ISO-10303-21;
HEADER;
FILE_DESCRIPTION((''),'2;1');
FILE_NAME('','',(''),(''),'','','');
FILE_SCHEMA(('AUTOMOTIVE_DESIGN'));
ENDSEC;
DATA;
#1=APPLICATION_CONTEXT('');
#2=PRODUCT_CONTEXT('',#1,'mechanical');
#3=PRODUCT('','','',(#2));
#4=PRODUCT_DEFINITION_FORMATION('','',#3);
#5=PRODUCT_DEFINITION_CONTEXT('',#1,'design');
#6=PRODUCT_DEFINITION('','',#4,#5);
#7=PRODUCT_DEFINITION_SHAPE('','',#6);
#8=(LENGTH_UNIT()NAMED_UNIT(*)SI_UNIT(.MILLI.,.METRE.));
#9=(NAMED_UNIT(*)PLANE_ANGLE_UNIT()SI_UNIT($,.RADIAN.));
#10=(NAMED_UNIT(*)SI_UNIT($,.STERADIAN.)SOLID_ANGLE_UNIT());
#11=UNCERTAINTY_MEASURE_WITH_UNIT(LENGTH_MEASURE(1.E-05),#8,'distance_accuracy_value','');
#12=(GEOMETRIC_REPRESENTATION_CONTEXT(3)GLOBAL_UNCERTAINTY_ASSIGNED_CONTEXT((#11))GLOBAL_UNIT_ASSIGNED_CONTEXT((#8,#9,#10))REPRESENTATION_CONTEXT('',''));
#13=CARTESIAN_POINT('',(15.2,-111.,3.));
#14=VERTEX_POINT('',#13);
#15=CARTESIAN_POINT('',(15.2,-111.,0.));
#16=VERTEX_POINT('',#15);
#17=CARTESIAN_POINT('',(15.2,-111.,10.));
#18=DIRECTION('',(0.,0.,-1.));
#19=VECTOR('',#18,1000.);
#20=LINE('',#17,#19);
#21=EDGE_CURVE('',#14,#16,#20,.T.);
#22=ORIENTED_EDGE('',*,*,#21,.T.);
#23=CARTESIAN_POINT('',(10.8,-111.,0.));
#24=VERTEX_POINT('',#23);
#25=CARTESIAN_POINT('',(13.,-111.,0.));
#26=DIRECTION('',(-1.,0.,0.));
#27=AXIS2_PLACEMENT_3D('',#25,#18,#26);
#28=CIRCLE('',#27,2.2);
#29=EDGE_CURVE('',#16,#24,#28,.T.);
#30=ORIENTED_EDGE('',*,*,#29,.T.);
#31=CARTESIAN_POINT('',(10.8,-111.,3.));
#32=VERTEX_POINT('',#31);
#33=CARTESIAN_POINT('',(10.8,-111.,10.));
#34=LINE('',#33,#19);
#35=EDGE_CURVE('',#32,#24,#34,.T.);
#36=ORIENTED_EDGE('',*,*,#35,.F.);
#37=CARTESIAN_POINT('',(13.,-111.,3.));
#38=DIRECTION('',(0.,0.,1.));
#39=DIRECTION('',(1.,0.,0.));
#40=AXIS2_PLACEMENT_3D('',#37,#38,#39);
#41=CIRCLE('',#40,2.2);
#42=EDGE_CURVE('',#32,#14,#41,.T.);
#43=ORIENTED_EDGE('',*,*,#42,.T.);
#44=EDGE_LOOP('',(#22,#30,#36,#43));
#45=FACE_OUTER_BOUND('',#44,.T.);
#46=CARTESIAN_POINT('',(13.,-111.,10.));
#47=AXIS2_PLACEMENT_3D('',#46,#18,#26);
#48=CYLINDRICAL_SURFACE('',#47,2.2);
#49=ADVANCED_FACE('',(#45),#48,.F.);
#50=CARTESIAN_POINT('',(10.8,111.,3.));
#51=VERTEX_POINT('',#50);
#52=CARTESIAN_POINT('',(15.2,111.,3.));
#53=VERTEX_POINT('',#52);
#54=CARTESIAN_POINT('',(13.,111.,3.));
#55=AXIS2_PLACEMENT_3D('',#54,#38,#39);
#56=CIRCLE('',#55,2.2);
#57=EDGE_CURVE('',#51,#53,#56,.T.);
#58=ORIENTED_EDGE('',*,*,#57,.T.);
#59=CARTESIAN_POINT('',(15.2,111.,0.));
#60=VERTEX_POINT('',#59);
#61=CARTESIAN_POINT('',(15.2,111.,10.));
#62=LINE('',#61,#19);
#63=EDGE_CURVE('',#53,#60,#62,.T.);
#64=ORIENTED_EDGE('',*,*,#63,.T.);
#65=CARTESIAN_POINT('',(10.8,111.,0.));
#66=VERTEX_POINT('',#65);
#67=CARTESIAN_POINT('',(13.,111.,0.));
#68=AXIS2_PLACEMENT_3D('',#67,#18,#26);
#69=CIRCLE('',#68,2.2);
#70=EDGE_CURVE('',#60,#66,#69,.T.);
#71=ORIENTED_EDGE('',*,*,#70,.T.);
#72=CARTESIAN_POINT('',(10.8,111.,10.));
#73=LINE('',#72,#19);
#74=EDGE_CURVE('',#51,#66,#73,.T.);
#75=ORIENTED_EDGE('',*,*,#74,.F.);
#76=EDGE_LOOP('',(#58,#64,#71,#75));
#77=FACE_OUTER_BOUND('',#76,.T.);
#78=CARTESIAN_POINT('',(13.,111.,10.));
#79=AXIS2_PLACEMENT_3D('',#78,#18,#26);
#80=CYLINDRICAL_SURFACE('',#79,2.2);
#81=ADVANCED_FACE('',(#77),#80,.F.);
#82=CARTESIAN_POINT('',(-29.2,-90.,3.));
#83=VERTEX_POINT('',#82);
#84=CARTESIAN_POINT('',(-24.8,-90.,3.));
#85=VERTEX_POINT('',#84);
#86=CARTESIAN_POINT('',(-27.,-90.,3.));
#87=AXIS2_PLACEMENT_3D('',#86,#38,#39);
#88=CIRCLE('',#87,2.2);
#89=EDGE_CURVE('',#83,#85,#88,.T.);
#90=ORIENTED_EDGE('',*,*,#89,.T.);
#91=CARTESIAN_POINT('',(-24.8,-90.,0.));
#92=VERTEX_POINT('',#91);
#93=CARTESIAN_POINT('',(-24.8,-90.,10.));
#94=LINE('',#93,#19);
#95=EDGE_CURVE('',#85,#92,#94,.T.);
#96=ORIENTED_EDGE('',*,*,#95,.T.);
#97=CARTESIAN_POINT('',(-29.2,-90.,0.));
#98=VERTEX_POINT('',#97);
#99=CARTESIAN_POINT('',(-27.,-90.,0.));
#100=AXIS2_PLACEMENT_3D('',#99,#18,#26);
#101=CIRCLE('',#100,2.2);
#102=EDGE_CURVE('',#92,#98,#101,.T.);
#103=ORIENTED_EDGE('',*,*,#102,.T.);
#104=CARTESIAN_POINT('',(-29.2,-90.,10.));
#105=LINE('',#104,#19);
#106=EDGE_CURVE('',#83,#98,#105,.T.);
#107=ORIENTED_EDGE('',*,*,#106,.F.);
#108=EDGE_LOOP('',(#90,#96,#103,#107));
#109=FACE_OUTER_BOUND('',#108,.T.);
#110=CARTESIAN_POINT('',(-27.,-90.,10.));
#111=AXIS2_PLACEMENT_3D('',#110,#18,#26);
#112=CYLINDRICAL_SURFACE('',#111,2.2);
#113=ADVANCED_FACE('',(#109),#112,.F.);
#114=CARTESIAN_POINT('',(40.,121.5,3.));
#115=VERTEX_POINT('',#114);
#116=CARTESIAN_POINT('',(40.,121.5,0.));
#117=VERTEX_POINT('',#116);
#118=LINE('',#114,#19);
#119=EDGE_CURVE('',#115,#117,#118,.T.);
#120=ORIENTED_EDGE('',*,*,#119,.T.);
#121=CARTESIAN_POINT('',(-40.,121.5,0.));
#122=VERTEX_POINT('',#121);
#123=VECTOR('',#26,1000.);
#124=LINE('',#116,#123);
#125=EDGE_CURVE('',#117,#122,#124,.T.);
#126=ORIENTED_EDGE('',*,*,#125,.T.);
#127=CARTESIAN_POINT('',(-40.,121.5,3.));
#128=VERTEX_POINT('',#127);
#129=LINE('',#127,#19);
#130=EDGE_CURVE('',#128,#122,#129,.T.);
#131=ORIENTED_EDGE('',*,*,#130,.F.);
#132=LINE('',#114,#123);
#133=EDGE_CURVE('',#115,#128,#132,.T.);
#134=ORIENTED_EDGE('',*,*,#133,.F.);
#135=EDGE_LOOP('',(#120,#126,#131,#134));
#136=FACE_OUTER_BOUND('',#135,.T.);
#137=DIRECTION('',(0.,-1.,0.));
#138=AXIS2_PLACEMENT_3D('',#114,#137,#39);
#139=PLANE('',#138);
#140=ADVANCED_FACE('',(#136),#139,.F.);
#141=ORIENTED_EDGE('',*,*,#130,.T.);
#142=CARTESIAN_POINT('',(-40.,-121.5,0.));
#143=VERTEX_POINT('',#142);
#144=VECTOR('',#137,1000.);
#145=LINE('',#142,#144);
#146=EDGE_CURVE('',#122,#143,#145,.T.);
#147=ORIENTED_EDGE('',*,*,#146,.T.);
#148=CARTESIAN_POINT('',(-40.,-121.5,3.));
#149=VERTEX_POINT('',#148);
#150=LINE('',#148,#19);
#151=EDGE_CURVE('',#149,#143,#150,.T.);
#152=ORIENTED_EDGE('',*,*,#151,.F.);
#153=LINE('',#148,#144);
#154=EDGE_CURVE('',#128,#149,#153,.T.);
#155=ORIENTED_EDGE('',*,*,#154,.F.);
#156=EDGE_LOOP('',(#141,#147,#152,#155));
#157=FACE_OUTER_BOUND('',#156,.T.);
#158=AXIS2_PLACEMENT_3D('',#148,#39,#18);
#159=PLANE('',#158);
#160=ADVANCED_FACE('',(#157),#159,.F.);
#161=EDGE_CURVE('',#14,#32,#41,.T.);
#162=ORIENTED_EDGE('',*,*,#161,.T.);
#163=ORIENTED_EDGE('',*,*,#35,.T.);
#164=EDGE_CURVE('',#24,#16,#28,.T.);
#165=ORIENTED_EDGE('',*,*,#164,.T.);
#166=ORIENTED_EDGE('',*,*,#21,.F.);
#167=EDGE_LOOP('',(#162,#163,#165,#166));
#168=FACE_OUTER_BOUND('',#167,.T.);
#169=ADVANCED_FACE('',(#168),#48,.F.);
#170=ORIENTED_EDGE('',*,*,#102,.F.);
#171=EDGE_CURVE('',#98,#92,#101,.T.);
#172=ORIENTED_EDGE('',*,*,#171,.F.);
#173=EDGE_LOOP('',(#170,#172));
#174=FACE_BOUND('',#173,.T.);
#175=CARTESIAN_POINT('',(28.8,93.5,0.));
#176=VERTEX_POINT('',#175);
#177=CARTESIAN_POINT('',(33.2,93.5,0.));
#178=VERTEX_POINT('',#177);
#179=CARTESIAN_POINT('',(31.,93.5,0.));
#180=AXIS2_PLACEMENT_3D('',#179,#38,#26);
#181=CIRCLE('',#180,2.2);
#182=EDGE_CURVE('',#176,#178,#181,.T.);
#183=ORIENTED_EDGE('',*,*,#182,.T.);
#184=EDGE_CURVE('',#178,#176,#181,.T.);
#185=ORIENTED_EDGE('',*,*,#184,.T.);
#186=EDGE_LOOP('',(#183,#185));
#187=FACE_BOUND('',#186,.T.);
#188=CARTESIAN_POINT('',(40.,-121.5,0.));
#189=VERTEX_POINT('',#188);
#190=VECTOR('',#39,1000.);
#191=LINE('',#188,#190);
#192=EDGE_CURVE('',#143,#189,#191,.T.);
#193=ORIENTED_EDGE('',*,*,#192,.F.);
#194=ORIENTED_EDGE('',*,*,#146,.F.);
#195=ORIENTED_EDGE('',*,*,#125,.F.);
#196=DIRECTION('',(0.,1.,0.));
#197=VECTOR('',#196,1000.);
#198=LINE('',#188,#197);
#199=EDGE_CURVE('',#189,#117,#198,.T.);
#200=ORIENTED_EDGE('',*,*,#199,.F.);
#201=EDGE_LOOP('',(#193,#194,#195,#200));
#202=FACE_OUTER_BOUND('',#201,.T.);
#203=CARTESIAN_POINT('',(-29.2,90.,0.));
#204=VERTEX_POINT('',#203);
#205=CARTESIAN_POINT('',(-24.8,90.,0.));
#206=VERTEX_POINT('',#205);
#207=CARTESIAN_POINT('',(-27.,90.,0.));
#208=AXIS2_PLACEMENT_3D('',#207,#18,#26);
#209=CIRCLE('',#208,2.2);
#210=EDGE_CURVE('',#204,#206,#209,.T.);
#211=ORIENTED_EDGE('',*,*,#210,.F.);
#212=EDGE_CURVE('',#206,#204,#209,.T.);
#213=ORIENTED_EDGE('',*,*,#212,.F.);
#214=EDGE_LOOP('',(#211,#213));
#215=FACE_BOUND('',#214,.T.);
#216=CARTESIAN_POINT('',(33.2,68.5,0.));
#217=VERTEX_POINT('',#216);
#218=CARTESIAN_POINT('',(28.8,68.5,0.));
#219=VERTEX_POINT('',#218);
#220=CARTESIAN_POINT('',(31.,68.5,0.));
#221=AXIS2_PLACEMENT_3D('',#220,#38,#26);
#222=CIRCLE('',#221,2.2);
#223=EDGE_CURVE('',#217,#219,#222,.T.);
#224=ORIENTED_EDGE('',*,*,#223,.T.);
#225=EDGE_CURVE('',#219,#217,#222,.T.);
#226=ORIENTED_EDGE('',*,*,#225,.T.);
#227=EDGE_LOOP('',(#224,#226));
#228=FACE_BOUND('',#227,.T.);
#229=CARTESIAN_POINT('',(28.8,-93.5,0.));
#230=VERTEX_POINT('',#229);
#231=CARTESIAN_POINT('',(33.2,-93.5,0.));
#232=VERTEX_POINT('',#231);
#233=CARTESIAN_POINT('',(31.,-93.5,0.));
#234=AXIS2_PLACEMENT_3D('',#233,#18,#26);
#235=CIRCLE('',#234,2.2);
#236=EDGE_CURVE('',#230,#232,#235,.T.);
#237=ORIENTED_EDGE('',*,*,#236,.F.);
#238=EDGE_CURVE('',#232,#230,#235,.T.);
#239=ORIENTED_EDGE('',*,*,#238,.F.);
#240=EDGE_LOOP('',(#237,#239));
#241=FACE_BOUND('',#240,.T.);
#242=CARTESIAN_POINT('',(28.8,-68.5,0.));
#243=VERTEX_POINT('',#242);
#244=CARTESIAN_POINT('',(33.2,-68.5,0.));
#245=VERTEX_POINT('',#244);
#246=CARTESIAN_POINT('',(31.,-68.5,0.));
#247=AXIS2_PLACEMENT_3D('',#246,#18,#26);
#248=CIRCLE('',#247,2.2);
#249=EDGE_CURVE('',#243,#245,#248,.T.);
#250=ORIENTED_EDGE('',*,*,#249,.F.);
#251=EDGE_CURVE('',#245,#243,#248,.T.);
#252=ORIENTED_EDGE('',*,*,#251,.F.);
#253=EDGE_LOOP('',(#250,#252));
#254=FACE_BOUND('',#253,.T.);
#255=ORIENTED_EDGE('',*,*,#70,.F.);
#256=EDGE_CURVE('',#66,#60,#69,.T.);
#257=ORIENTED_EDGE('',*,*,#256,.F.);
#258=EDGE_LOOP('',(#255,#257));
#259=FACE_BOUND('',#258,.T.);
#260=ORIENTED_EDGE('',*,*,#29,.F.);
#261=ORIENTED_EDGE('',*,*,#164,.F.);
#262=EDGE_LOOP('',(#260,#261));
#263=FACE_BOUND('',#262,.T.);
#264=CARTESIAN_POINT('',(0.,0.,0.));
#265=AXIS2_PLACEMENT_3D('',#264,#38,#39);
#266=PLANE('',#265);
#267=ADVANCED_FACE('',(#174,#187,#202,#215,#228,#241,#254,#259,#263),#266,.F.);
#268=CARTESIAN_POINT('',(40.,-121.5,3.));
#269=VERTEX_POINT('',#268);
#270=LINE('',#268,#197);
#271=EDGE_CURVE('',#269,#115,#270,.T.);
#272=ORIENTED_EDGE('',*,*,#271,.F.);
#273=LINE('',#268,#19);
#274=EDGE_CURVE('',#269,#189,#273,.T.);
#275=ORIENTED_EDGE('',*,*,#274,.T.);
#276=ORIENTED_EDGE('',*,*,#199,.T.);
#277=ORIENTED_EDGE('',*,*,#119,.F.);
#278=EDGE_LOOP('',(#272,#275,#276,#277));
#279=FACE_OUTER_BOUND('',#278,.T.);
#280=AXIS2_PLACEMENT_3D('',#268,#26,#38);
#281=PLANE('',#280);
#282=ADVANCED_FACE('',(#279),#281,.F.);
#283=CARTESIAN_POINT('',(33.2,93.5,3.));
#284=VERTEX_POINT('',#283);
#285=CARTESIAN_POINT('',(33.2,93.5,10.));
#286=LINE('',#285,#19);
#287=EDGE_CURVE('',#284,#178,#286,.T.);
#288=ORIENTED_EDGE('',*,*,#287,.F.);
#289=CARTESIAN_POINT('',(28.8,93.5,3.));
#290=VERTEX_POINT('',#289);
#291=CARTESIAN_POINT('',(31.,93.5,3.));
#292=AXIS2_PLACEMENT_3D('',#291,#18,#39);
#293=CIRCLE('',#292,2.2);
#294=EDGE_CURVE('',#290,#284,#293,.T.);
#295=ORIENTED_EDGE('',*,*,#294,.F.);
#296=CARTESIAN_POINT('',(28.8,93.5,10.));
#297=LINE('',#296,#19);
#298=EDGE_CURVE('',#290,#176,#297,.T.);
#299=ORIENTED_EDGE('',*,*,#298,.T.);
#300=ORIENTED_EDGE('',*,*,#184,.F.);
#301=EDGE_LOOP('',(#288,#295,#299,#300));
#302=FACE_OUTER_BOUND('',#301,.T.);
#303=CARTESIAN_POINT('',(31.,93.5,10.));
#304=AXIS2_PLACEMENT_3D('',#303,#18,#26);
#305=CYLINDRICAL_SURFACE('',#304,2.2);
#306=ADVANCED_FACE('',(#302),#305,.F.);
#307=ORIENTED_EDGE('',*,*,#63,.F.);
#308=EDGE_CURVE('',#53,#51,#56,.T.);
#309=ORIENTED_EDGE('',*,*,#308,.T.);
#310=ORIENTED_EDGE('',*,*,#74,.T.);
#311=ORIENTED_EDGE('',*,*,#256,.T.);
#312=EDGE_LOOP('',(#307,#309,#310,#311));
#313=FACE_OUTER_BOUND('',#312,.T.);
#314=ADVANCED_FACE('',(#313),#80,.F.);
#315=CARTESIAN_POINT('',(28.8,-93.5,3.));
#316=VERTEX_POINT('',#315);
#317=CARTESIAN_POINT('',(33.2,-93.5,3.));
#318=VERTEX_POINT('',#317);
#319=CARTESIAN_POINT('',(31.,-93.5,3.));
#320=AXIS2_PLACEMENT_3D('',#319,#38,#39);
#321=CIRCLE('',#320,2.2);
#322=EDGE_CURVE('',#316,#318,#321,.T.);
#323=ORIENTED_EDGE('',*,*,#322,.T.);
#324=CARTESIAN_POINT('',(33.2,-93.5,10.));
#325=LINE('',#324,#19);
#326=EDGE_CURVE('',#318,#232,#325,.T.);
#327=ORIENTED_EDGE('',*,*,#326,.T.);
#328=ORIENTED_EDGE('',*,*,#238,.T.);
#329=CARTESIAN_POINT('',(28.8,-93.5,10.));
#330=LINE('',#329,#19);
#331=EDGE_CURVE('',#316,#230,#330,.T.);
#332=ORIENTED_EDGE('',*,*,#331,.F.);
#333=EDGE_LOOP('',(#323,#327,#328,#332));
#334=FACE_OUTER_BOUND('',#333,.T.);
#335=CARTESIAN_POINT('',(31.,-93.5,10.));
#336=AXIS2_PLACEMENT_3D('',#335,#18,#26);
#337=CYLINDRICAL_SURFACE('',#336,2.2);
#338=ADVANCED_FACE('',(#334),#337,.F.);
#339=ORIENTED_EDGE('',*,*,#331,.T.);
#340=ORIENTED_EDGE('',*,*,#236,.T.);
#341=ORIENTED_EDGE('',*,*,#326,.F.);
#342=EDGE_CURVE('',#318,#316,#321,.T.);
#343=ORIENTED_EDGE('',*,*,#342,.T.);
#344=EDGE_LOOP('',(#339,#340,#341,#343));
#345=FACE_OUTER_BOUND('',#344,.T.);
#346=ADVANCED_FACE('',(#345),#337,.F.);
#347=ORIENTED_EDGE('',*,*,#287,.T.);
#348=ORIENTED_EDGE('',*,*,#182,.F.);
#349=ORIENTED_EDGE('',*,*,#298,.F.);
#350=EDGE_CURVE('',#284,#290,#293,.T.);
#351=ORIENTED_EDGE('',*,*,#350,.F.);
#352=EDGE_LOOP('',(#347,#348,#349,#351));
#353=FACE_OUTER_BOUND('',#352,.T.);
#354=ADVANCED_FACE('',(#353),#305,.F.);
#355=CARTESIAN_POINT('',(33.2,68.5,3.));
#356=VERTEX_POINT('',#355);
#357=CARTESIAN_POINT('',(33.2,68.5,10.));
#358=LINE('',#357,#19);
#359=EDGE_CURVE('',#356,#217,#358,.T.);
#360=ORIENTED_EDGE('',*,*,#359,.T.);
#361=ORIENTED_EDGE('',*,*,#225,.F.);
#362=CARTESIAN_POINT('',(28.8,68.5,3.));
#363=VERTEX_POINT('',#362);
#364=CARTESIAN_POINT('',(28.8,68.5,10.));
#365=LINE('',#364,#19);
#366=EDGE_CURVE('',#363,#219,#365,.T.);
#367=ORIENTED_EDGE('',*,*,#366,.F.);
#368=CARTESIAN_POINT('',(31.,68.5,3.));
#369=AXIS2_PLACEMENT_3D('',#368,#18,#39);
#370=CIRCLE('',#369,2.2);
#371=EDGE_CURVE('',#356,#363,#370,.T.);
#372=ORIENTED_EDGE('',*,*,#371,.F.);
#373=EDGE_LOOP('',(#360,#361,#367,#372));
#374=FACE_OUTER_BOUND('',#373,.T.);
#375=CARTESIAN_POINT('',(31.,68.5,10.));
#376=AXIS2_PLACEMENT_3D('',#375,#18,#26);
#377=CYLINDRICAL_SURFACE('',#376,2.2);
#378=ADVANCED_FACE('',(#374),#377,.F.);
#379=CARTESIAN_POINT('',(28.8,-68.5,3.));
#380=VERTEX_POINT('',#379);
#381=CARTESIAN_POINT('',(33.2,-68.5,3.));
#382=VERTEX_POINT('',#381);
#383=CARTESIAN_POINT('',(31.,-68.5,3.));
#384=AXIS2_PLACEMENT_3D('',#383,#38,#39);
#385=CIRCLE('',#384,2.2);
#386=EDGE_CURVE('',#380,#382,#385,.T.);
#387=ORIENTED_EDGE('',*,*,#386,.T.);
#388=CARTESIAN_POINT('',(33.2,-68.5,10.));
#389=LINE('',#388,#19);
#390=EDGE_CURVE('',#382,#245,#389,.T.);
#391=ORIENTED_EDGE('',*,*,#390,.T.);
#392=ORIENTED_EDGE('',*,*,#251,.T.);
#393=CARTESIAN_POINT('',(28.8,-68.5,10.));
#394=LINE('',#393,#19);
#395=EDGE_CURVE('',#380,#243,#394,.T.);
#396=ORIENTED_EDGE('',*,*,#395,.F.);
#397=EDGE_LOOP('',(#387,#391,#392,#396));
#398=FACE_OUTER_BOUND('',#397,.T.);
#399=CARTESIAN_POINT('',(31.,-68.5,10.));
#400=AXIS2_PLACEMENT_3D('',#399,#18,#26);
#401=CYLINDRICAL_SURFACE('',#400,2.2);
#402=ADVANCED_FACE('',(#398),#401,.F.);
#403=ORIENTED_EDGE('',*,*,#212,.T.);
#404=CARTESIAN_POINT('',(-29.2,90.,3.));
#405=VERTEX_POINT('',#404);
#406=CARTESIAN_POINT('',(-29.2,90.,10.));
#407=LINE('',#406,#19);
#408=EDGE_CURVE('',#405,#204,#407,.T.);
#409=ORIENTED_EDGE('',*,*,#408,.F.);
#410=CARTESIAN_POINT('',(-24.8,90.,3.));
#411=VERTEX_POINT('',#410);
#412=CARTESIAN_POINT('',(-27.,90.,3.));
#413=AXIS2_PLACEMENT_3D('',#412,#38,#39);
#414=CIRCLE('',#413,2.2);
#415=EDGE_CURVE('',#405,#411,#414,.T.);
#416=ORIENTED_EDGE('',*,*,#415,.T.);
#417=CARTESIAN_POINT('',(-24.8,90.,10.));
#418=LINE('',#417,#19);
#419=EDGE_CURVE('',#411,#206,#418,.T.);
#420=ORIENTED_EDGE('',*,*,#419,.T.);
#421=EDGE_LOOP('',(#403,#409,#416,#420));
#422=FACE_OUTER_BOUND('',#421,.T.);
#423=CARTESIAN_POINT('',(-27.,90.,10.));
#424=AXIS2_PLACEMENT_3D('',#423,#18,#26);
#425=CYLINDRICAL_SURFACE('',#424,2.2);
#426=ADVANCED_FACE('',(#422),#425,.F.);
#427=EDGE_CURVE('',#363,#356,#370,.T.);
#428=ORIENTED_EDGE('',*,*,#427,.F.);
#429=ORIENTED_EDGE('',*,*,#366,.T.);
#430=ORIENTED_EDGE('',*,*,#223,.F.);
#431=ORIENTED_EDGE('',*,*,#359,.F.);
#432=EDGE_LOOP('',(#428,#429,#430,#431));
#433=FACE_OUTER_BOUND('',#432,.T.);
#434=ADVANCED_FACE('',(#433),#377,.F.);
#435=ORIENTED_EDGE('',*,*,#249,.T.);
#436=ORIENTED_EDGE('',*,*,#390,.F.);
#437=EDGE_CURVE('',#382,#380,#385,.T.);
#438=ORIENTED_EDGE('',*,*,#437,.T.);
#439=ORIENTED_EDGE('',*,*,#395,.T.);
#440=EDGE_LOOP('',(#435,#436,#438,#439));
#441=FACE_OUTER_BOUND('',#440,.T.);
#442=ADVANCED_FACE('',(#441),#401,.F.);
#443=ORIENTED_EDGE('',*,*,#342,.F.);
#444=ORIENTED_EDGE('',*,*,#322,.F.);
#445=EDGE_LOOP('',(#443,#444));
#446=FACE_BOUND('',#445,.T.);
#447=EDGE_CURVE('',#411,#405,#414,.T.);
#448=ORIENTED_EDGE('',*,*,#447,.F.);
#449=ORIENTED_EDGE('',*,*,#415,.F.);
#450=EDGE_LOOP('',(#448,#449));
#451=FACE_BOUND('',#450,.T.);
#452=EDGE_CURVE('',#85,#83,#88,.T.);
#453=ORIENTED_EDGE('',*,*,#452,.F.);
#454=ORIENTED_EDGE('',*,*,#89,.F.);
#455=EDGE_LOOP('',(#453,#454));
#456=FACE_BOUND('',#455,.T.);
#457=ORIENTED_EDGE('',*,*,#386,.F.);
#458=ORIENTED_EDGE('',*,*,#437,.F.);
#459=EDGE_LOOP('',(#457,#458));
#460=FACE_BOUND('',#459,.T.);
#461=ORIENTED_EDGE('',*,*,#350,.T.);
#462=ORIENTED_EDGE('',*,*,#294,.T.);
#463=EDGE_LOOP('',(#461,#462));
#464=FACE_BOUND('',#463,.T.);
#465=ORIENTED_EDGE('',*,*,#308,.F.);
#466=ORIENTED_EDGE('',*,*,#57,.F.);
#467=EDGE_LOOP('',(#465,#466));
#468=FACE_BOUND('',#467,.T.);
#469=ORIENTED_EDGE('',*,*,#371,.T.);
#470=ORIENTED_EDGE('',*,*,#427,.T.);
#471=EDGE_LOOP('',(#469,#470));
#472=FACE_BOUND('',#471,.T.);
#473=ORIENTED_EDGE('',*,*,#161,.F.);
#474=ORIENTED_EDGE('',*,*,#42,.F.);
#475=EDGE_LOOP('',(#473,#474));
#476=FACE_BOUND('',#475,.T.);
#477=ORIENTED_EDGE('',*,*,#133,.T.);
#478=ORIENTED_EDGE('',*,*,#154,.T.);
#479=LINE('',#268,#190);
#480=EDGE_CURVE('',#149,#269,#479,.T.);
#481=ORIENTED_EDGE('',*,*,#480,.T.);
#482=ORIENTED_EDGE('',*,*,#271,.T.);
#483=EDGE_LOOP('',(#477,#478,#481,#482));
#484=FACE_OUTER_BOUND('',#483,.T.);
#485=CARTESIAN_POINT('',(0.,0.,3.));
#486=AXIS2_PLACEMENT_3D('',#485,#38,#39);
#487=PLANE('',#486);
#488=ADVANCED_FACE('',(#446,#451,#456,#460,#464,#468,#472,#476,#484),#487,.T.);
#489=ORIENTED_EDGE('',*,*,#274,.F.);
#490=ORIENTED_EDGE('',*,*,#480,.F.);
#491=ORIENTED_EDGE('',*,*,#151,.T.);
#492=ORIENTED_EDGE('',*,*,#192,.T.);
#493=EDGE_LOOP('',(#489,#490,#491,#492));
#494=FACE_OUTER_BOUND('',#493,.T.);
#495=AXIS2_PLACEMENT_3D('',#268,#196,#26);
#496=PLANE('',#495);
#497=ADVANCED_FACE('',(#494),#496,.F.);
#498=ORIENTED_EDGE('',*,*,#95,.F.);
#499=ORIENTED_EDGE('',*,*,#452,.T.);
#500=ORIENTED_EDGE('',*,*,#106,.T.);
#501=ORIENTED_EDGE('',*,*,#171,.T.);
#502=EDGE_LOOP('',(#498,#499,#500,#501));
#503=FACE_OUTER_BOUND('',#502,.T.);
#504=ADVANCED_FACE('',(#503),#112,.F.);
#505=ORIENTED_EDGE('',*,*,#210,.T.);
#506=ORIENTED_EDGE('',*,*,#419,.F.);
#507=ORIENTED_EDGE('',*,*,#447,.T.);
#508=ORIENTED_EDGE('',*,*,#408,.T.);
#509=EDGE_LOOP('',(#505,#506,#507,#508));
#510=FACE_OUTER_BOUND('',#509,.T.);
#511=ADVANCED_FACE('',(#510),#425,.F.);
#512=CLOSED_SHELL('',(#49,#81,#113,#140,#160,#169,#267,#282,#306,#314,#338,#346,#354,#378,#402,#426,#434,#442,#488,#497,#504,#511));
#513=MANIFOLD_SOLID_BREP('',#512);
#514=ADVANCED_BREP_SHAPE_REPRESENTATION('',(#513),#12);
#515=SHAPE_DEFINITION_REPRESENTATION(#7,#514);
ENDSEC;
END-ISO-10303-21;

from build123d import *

# Parameters (mm, degrees)
SKETCH_1_W          = 80
SKETCH_1_H          = 243
EXTRUDE_1_DEPTH     = 3
SKETCH_4_R          = 2.2
CUT_EXTRUDE_2_DEPTH = 10
SKETCH_5_R          = 2.2
CUT_EXTRUDE_3_DEPTH = 10


with BuildPart() as part:
    # 草图1 → 凸台-拉伸1 (new body)
    with BuildSketch(Plane.XY):
        Rectangle(SKETCH_1_W, SKETCH_1_H)
    extrude(amount=EXTRUDE_1_DEPTH)

    # 草图4 → 切除-拉伸2 (cut)
    with BuildSketch(Plane(origin=(0, 0, 0), x_dir=(-1, 0, 0), z_dir=(0, 0, -1))):
        with Locations((-31, -68.5)):
            Circle(SKETCH_4_R)
        with Locations((-31, -93.5)):
            Circle(SKETCH_4_R)
    cut_extrude_2 = extrude(amount=-CUT_EXTRUDE_2_DEPTH, mode=Mode.SUBTRACT)

    # 镜向1: 切除-拉伸2 across plane
    add(cut_extrude_2.mirror(Plane.ZX), mode=Mode.SUBTRACT)

    # 草图5 → 切除-拉伸3 (cut)
    with BuildSketch(Plane(origin=(0, 0, 0), x_dir=(-1, 0, 0), z_dir=(0, 0, -1))):
        with Locations((-13, 111)):
            Circle(SKETCH_5_R)
        with Locations((-13, -111)):
            Circle(SKETCH_5_R)
        with Locations((27, 90)):
            Circle(SKETCH_5_R)
        with Locations((27, -90)):
            Circle(SKETCH_5_R)
    extrude(amount=-CUT_EXTRUDE_3_DEPTH, mode=Mode.SUBTRACT)


solid = part.part
